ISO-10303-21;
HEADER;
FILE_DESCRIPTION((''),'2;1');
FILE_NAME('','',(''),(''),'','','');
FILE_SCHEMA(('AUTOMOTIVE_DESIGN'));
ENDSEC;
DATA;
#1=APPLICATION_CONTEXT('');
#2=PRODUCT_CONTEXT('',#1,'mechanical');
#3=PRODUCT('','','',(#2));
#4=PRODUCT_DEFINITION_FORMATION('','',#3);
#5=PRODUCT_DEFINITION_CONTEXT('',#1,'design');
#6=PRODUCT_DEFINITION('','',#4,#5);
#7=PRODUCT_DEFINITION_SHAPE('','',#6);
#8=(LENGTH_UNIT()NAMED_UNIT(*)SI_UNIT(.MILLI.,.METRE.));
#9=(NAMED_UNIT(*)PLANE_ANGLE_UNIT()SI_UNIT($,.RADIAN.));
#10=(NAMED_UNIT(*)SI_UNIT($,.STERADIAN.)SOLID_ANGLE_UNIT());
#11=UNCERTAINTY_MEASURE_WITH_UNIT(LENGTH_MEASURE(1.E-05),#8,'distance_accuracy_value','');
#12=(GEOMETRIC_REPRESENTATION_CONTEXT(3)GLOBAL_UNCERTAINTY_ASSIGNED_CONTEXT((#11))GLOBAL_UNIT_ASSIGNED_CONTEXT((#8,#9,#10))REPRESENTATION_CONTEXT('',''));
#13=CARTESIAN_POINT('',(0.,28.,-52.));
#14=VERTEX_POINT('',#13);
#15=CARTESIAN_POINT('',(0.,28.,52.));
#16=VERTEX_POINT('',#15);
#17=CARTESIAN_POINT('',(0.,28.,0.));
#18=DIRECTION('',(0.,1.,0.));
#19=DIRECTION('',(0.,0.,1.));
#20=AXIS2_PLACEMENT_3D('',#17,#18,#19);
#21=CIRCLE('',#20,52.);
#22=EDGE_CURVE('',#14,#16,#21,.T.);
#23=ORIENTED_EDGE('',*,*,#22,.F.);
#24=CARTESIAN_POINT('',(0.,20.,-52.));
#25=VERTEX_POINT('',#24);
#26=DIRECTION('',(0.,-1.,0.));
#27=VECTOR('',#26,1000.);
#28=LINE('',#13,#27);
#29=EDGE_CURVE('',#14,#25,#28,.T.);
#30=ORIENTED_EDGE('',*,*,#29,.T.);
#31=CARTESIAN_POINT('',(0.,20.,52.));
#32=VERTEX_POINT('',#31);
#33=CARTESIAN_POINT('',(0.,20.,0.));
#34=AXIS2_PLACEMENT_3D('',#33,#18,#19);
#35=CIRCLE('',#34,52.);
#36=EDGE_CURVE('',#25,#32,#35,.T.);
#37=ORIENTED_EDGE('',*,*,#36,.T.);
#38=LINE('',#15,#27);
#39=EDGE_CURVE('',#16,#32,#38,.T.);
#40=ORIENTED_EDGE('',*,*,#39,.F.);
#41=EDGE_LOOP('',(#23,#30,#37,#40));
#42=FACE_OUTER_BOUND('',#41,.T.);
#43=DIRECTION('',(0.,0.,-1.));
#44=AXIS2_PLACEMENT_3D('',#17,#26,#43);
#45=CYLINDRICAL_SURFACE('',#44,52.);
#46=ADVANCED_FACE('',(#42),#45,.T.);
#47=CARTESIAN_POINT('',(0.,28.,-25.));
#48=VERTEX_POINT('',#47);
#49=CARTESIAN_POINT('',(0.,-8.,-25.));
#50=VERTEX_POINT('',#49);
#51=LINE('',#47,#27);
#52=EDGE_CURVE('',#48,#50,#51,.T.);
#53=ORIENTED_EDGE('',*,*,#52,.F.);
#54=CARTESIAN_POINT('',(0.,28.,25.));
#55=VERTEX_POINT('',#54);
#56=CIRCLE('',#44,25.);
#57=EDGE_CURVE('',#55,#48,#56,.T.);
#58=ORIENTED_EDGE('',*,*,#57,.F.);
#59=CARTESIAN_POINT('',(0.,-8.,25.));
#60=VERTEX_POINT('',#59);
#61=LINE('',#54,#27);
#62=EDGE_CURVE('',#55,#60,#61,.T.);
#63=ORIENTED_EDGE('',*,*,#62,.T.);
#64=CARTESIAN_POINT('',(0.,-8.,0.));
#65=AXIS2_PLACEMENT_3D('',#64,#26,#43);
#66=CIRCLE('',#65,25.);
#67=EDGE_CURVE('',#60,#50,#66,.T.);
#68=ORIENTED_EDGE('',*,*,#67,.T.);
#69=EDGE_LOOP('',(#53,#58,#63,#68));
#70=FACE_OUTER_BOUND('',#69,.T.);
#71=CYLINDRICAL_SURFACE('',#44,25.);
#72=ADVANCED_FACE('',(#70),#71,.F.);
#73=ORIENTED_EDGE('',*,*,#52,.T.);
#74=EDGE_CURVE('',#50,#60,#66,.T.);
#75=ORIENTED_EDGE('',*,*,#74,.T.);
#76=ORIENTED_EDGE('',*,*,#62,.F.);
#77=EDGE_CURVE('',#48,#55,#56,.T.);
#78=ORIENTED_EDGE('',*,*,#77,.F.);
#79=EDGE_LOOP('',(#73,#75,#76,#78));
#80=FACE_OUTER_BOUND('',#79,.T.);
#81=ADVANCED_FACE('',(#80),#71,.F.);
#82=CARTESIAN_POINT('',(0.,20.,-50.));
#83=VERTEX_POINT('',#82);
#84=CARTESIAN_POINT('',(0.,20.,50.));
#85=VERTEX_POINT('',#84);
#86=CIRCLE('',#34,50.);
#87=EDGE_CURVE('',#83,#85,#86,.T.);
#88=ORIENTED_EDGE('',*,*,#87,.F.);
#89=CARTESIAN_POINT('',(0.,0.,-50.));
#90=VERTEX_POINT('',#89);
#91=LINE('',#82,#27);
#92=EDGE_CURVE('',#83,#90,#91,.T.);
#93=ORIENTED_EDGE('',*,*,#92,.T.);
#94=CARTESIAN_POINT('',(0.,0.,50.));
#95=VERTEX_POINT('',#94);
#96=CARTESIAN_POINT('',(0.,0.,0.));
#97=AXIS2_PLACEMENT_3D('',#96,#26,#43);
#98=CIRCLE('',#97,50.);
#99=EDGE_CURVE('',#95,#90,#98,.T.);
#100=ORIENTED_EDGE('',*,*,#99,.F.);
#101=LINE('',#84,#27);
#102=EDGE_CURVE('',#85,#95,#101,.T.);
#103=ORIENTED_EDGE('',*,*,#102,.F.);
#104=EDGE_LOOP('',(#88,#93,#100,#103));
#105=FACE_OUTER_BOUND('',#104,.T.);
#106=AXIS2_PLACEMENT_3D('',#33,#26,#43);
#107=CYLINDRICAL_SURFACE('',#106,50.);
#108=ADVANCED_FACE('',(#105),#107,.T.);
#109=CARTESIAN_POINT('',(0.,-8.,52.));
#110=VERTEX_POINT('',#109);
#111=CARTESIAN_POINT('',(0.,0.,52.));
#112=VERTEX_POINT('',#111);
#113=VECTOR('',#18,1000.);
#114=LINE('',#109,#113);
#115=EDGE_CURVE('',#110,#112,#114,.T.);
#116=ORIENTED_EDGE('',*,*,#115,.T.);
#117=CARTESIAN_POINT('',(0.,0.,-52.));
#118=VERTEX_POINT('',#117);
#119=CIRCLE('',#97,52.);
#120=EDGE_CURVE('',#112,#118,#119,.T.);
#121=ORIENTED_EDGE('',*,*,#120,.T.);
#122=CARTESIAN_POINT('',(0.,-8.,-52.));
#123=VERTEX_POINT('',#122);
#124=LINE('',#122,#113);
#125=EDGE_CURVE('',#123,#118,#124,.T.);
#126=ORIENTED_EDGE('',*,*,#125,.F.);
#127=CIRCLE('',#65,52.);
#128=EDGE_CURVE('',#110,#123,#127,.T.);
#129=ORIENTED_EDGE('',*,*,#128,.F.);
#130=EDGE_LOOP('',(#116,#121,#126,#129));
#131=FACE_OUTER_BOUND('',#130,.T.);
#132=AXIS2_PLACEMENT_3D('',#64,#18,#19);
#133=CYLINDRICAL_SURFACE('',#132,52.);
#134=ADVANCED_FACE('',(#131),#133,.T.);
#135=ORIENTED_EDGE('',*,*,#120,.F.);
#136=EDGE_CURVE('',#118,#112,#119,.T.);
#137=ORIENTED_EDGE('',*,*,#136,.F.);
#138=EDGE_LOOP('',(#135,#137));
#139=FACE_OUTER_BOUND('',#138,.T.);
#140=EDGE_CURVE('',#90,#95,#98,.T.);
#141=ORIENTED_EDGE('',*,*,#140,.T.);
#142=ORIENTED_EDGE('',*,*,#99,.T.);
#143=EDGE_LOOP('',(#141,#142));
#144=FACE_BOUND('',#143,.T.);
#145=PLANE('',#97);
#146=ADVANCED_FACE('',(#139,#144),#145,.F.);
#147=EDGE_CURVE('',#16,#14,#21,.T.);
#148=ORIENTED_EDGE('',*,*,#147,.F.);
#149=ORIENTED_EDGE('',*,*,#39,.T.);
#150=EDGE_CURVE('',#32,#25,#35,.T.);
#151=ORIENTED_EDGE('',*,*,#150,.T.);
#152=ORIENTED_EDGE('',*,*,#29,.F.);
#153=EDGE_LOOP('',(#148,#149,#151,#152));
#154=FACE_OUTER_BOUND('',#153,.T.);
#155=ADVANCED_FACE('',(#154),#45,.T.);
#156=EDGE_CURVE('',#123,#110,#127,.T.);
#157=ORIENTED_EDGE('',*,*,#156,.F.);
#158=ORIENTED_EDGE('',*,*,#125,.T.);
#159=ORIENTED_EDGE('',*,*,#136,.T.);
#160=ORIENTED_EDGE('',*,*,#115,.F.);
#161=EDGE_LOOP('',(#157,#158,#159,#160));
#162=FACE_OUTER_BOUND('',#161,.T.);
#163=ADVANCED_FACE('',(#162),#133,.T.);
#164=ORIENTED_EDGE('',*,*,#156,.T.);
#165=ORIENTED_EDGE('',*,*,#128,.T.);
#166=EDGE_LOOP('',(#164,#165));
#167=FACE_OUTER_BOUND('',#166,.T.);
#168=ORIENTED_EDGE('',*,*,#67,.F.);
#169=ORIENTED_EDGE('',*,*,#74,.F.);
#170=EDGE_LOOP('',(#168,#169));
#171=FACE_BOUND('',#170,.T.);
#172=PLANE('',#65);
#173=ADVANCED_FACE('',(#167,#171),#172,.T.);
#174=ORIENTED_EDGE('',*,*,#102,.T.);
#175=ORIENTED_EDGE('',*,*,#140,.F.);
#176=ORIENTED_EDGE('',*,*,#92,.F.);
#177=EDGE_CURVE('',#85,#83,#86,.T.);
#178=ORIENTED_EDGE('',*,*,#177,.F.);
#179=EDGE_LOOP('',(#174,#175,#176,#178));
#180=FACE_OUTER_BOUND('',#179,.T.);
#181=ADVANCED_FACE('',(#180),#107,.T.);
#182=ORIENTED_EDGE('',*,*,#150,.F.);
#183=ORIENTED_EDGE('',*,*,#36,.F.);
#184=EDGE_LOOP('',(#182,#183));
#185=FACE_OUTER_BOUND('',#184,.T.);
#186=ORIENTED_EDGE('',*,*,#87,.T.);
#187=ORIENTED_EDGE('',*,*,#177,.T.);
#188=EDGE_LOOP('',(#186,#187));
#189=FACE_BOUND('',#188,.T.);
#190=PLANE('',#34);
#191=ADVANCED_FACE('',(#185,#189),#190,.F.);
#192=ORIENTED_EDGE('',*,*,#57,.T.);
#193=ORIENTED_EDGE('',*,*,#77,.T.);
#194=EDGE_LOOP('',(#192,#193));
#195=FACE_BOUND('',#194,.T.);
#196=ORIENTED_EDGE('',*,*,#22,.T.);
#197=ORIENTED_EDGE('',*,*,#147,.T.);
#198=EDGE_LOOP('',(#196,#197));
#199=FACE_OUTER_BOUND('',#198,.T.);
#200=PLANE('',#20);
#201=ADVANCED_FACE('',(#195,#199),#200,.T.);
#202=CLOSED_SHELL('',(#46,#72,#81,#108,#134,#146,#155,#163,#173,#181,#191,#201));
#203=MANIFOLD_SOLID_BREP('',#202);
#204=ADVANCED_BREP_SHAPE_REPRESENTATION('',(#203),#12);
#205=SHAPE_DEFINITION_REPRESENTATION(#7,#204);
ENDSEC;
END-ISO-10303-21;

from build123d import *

# Parameters (mm, degrees)
SKETCH1_R           = 50
BOSS_EXTRUDE1_DEPTH = 20
SKETCH2_R           = 52
BOSS_EXTRUDE2_DEPTH = 8
BOSS_EXTRUDE3_START = 8
SKETCH3_R           = 52
BOSS_EXTRUDE3_DEPTH = 8
SKETCH4_R           = 25
CUT_EXTRUDE1_DEPTH  = 82.877957962


with BuildPart() as part:
    # Sketch1 → Boss-Extrude1 (new body)
    with BuildSketch(Plane(origin=(0, 0, 0), x_dir=(1, 0, 0), z_dir=(0, 1, 0))):
        with Locations(Location((0, 0, 0), (0, 0, 270))):
            Circle(SKETCH1_R)
    extrude(amount=BOSS_EXTRUDE1_DEPTH)

    # Sketch2 → Boss-Extrude2 (add)
    with BuildSketch(Plane(origin=(0, 20, 0), x_dir=(1, 0, 0), z_dir=(0, 1, 0))):
        with Locations(Location((0, 0, 0), (0, 0, 270))):
            Circle(SKETCH2_R)
    extrude(amount=BOSS_EXTRUDE2_DEPTH)

    # Sketch3 → Boss-Extrude3 (add)
    with BuildSketch(Plane.XZ.offset(BOSS_EXTRUDE3_START)):
        with Locations(Location((0, 0, 0), (0, 0, 90))):
            Circle(SKETCH3_R)
    extrude(amount=-BOSS_EXTRUDE3_DEPTH)

    # Sketch4 → Cut-Extrude1 (cut, through all)
    with BuildSketch(Plane.XZ.offset(8)):
        with Locations(Location((0, 0, 0), (0, 0, 270))):
            Circle(SKETCH4_R)
    extrude(amount=-CUT_EXTRUDE1_DEPTH, mode=Mode.SUBTRACT)


solid = part.part
